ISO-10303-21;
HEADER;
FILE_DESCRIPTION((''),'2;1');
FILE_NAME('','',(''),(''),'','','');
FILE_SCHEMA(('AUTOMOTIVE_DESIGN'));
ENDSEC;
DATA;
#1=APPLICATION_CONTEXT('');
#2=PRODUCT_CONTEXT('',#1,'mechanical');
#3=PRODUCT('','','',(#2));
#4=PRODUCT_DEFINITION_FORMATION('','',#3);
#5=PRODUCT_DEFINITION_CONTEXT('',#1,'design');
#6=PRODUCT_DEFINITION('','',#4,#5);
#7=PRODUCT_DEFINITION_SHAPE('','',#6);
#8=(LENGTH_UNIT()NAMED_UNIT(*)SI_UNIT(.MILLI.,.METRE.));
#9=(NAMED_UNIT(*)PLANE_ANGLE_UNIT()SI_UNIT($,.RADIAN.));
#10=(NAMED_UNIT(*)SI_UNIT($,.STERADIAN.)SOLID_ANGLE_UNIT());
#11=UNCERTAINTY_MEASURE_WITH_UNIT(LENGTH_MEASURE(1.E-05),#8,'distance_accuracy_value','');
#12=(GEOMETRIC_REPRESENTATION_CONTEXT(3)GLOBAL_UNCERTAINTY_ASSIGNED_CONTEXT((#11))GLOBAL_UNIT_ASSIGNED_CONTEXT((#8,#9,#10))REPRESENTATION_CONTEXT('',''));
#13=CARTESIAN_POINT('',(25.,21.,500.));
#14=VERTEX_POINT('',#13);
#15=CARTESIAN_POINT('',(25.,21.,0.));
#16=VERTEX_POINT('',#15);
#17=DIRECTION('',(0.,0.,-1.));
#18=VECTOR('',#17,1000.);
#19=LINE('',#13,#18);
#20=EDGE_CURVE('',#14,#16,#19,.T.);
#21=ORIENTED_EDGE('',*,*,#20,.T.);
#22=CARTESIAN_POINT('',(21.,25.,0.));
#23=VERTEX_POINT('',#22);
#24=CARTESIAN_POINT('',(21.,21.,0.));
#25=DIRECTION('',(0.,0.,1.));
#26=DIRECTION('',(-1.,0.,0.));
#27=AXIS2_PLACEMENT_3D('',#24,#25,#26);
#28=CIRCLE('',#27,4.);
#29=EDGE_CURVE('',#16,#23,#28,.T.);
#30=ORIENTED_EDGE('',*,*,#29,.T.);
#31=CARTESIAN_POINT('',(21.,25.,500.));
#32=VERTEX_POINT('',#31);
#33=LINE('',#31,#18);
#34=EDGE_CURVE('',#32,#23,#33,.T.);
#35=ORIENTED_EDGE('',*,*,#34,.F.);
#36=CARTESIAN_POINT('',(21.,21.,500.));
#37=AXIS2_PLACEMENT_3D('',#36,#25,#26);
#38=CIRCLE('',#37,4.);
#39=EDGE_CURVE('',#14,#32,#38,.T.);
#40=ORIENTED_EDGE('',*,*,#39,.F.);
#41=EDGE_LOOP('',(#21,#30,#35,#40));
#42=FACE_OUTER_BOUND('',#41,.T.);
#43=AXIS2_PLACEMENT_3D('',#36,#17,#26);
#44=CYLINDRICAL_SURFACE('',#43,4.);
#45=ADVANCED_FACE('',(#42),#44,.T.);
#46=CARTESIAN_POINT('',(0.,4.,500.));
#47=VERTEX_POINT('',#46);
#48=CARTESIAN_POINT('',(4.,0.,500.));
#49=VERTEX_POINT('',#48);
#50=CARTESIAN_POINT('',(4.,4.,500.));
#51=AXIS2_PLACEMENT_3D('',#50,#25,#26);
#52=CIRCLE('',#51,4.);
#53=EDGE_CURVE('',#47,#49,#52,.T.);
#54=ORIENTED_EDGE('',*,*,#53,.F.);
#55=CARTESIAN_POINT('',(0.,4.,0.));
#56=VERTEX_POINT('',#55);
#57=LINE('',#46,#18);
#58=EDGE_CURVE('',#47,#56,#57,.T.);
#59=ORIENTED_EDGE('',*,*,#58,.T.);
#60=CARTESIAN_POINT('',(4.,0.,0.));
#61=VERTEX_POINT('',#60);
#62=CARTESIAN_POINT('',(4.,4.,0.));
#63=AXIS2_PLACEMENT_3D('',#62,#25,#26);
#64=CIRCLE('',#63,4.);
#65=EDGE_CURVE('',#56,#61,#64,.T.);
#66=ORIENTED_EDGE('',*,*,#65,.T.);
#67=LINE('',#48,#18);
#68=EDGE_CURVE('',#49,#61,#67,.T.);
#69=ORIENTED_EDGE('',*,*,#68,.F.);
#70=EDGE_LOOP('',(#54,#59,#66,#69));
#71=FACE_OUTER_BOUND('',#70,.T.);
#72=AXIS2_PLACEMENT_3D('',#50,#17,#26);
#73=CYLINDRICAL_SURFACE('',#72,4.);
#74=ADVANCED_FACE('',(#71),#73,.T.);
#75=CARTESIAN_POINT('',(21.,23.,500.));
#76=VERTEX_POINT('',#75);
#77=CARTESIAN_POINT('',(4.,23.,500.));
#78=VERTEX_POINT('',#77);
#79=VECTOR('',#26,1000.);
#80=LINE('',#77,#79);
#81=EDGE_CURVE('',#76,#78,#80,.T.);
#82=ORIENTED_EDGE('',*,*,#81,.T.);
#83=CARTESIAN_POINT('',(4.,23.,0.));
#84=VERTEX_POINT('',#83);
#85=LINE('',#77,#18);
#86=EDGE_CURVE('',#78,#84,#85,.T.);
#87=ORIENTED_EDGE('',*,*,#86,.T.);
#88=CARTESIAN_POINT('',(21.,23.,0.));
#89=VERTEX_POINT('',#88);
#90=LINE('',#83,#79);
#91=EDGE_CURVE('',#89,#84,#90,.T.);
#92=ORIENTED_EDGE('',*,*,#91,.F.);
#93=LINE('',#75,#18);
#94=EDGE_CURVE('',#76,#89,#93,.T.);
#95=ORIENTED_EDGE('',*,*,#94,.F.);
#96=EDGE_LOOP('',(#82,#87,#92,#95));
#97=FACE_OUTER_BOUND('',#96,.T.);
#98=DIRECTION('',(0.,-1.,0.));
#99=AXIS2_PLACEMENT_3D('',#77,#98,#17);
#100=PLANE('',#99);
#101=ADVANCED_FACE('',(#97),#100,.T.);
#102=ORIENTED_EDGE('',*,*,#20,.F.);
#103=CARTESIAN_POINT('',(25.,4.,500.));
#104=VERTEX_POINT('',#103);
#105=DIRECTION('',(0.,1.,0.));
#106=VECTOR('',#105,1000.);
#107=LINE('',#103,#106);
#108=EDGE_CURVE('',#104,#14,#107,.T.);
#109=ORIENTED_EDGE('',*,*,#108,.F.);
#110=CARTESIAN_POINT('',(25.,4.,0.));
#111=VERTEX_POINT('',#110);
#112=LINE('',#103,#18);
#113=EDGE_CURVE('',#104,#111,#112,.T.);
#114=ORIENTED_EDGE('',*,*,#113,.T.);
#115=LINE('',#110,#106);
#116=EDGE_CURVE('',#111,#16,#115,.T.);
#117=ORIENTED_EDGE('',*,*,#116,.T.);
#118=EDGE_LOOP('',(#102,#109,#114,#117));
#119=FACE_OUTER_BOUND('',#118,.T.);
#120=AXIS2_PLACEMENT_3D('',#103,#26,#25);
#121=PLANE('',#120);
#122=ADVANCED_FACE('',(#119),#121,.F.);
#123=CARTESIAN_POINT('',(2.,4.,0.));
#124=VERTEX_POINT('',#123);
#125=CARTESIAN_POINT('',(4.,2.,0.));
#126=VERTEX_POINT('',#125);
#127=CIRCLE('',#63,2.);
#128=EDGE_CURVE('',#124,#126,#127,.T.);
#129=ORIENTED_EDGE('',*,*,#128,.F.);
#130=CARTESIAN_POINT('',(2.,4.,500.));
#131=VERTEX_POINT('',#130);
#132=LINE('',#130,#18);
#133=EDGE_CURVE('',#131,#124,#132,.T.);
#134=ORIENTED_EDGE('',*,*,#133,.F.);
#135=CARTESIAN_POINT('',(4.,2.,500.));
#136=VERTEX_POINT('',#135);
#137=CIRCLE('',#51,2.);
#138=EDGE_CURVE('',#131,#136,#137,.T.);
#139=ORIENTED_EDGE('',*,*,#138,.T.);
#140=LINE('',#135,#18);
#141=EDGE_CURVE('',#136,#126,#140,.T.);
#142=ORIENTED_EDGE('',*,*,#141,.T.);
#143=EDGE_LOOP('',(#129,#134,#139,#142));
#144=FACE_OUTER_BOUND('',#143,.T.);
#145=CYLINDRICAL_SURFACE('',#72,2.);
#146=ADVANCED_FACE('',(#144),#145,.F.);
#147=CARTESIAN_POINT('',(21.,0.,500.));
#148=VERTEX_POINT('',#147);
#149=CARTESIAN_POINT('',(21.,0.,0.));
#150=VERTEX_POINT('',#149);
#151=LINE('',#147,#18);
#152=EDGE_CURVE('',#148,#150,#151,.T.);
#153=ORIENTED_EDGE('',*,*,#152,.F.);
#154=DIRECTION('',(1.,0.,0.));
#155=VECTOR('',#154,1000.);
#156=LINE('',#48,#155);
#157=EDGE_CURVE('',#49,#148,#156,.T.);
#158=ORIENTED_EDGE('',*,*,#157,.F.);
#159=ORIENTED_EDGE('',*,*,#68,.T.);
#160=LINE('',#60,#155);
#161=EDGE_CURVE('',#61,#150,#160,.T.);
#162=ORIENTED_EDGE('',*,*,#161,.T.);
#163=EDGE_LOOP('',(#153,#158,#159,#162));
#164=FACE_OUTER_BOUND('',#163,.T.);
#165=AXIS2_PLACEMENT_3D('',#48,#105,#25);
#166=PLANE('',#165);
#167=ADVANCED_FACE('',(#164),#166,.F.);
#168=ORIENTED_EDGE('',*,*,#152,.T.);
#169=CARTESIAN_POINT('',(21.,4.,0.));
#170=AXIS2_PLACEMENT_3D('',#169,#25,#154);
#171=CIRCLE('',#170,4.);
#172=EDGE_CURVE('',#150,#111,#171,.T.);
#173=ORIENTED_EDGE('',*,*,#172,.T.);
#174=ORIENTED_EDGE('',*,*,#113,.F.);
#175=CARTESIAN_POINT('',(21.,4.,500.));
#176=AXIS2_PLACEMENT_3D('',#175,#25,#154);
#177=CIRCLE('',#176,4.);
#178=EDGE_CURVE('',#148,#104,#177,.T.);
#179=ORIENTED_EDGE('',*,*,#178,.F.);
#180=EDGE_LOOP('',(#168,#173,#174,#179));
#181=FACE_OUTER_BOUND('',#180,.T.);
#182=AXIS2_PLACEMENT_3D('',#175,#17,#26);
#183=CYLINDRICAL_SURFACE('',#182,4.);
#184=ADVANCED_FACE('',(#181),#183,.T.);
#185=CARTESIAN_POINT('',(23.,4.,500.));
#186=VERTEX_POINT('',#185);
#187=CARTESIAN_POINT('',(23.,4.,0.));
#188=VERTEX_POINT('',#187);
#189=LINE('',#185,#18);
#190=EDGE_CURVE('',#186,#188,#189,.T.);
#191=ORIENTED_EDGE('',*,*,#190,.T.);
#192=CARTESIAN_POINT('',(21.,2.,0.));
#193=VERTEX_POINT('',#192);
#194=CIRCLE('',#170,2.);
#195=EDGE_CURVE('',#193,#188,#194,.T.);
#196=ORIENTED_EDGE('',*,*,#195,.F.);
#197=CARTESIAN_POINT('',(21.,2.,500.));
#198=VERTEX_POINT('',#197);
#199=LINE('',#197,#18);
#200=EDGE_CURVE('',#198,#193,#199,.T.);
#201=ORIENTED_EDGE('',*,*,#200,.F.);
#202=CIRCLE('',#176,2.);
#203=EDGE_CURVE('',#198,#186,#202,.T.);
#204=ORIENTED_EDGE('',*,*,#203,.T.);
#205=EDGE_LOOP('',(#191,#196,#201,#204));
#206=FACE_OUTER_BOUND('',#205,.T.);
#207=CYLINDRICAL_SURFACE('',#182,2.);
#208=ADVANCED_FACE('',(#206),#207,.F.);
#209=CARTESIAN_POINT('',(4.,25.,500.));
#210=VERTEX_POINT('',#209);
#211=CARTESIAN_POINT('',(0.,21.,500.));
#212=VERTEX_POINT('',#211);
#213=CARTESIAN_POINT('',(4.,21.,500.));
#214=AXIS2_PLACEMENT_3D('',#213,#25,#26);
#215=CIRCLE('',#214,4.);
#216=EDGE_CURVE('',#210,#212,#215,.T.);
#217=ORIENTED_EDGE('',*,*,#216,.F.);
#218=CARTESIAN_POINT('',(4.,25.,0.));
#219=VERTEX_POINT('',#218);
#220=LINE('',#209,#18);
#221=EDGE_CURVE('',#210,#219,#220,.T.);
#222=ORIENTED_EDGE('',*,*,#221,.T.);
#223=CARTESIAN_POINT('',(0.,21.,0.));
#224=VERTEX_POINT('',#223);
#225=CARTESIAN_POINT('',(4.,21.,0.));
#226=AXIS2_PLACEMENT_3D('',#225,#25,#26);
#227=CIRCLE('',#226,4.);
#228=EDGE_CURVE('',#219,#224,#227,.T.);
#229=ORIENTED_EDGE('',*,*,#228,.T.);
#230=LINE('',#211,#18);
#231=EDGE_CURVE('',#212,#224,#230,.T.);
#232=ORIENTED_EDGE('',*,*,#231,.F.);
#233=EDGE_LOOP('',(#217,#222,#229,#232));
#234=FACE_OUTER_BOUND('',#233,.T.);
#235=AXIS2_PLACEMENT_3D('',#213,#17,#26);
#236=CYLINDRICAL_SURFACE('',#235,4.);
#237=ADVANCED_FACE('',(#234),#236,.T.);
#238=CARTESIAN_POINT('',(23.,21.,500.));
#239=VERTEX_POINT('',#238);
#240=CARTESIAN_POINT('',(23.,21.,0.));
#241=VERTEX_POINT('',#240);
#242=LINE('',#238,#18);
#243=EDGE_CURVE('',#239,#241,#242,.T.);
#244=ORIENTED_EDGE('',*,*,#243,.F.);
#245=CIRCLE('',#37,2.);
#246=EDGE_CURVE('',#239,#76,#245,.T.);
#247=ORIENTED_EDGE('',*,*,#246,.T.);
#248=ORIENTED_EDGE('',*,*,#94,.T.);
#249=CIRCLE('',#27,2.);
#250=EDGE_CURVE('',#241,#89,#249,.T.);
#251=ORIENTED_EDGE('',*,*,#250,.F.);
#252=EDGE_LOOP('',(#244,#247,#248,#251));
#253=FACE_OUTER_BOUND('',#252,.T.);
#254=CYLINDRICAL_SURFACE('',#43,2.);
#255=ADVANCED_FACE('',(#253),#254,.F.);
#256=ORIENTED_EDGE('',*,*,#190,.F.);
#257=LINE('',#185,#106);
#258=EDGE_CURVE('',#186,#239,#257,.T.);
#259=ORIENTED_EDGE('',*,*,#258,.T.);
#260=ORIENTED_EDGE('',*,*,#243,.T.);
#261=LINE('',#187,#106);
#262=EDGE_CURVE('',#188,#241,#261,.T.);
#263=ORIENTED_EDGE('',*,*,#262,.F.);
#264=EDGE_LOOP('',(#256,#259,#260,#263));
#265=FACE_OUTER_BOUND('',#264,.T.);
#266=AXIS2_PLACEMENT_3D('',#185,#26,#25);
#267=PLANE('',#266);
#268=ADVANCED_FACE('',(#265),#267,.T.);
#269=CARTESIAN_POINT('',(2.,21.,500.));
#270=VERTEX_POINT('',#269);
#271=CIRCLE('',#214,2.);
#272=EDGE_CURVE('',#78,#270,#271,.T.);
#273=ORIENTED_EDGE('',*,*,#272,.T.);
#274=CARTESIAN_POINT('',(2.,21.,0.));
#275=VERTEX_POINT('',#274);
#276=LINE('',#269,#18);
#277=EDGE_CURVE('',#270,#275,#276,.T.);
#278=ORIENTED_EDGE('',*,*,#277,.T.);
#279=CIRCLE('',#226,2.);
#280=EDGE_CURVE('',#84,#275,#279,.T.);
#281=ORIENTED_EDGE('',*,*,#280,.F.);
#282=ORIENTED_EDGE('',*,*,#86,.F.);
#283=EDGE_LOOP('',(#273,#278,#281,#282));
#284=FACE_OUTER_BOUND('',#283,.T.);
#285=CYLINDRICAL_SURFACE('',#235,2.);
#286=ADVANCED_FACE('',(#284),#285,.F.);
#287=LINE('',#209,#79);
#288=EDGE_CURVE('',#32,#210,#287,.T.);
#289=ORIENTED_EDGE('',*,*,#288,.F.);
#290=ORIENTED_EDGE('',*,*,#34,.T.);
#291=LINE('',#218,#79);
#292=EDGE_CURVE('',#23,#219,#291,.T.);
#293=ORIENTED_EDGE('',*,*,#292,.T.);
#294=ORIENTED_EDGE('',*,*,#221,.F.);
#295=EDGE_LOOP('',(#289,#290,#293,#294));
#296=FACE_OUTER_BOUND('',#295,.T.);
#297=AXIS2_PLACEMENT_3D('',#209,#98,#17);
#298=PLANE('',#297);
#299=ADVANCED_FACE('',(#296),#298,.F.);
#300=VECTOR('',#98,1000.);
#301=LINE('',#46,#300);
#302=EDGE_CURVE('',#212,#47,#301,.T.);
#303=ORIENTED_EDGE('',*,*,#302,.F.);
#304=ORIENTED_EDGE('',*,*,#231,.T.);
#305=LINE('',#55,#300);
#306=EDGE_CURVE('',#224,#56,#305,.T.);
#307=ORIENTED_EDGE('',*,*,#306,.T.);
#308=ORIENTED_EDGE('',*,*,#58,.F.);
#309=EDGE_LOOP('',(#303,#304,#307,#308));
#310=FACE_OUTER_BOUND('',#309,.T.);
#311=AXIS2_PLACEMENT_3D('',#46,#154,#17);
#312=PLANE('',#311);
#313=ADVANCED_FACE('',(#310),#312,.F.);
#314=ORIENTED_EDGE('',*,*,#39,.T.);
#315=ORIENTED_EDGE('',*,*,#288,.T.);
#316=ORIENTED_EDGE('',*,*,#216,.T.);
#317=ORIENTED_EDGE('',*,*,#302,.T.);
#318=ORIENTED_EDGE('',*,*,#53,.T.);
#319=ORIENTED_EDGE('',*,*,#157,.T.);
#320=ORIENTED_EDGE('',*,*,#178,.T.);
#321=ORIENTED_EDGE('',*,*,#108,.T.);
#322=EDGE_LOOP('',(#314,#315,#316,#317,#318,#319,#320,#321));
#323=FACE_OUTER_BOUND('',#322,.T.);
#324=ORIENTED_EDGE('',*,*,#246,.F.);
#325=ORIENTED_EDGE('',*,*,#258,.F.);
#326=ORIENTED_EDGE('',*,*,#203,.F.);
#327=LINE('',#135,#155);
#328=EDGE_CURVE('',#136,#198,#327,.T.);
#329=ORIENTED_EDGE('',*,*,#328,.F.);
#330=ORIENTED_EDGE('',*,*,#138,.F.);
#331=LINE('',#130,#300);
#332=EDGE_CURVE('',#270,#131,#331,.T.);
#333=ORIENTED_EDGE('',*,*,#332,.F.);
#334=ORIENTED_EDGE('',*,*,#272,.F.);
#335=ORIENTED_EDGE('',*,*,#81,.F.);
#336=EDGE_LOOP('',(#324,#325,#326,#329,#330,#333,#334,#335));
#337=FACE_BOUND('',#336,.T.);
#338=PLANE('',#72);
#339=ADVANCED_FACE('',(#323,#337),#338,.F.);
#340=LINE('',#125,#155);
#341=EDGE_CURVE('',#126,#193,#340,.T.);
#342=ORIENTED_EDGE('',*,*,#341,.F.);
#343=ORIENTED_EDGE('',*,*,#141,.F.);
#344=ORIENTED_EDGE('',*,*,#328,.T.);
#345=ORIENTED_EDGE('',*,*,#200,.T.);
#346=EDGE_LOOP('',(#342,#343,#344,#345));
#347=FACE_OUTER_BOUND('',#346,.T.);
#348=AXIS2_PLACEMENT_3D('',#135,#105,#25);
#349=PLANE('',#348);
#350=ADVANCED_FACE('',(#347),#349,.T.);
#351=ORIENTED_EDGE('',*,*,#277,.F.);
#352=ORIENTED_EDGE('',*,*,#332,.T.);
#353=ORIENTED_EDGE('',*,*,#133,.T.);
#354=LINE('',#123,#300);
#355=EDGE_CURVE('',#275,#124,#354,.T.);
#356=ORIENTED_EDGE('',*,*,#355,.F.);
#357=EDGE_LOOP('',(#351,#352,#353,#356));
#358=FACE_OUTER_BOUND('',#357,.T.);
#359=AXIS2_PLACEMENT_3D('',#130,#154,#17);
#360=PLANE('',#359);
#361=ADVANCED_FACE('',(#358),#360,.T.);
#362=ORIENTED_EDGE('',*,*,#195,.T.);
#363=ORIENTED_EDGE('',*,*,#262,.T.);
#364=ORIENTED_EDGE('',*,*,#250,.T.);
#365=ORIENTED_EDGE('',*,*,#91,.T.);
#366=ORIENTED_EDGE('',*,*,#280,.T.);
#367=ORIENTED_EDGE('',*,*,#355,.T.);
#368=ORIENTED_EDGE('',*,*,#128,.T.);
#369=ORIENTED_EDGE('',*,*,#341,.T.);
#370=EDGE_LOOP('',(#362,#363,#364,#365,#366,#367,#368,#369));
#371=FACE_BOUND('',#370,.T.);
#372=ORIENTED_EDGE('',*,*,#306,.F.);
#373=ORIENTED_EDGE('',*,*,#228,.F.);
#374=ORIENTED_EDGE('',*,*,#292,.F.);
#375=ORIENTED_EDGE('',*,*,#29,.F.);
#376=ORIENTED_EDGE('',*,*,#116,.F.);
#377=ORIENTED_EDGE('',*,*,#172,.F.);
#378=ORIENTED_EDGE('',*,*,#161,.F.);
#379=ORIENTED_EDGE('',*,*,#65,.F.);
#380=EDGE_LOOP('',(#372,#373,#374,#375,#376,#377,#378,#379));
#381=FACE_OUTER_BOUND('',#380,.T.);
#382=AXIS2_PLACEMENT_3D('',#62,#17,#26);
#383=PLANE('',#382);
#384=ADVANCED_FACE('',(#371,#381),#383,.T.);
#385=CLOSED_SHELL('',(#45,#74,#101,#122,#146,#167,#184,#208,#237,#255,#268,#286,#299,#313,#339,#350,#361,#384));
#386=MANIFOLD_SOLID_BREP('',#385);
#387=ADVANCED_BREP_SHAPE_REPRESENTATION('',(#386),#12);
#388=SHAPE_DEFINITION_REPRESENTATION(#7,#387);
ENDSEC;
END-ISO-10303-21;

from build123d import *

# Parameters (mm, degrees)
BOSS_EXTRUDE1_DEPTH = 500


with BuildPart() as part:
    # Sketch1 → Boss-Extrude1 (new body)
    with BuildSketch(Plane.XY):
        with BuildLine():
            Line((4, 0), (21, 0))
            ThreePointArc((21, 0), (23.828427125, 1.171572875), (25, 4))
            Line((25, 4), (25, 21))
            ThreePointArc((25, 21), (23.828427125, 23.828427125), (21, 25))
            Line((21, 25), (4, 25))
            ThreePointArc((4, 25), (1.171572875, 23.828427125), (0, 21))
            Line((0, 21), (0, 4))
            ThreePointArc((0, 4), (1.171572875, 1.171572875), (4, 0))
        make_face()
        with BuildLine():
            Line((23, 4), (23, 21))
            ThreePointArc((23, 21), (22.414213562, 22.414213562), (21, 23))
            Line((21, 23), (4, 23))
            ThreePointArc((4, 23), (2.585786438, 22.414213562), (2, 21))
            Line((2, 21), (2, 4))
            ThreePointArc((2, 4), (2.585786438, 2.585786438), (4, 2))
            Line((4, 2), (21, 2))
            ThreePointArc((21, 2), (22.414213562, 2.585786438), (23, 4))
        make_face(mode=Mode.SUBTRACT)
    extrude(amount=BOSS_EXTRUDE1_DEPTH)


solid = part.part
